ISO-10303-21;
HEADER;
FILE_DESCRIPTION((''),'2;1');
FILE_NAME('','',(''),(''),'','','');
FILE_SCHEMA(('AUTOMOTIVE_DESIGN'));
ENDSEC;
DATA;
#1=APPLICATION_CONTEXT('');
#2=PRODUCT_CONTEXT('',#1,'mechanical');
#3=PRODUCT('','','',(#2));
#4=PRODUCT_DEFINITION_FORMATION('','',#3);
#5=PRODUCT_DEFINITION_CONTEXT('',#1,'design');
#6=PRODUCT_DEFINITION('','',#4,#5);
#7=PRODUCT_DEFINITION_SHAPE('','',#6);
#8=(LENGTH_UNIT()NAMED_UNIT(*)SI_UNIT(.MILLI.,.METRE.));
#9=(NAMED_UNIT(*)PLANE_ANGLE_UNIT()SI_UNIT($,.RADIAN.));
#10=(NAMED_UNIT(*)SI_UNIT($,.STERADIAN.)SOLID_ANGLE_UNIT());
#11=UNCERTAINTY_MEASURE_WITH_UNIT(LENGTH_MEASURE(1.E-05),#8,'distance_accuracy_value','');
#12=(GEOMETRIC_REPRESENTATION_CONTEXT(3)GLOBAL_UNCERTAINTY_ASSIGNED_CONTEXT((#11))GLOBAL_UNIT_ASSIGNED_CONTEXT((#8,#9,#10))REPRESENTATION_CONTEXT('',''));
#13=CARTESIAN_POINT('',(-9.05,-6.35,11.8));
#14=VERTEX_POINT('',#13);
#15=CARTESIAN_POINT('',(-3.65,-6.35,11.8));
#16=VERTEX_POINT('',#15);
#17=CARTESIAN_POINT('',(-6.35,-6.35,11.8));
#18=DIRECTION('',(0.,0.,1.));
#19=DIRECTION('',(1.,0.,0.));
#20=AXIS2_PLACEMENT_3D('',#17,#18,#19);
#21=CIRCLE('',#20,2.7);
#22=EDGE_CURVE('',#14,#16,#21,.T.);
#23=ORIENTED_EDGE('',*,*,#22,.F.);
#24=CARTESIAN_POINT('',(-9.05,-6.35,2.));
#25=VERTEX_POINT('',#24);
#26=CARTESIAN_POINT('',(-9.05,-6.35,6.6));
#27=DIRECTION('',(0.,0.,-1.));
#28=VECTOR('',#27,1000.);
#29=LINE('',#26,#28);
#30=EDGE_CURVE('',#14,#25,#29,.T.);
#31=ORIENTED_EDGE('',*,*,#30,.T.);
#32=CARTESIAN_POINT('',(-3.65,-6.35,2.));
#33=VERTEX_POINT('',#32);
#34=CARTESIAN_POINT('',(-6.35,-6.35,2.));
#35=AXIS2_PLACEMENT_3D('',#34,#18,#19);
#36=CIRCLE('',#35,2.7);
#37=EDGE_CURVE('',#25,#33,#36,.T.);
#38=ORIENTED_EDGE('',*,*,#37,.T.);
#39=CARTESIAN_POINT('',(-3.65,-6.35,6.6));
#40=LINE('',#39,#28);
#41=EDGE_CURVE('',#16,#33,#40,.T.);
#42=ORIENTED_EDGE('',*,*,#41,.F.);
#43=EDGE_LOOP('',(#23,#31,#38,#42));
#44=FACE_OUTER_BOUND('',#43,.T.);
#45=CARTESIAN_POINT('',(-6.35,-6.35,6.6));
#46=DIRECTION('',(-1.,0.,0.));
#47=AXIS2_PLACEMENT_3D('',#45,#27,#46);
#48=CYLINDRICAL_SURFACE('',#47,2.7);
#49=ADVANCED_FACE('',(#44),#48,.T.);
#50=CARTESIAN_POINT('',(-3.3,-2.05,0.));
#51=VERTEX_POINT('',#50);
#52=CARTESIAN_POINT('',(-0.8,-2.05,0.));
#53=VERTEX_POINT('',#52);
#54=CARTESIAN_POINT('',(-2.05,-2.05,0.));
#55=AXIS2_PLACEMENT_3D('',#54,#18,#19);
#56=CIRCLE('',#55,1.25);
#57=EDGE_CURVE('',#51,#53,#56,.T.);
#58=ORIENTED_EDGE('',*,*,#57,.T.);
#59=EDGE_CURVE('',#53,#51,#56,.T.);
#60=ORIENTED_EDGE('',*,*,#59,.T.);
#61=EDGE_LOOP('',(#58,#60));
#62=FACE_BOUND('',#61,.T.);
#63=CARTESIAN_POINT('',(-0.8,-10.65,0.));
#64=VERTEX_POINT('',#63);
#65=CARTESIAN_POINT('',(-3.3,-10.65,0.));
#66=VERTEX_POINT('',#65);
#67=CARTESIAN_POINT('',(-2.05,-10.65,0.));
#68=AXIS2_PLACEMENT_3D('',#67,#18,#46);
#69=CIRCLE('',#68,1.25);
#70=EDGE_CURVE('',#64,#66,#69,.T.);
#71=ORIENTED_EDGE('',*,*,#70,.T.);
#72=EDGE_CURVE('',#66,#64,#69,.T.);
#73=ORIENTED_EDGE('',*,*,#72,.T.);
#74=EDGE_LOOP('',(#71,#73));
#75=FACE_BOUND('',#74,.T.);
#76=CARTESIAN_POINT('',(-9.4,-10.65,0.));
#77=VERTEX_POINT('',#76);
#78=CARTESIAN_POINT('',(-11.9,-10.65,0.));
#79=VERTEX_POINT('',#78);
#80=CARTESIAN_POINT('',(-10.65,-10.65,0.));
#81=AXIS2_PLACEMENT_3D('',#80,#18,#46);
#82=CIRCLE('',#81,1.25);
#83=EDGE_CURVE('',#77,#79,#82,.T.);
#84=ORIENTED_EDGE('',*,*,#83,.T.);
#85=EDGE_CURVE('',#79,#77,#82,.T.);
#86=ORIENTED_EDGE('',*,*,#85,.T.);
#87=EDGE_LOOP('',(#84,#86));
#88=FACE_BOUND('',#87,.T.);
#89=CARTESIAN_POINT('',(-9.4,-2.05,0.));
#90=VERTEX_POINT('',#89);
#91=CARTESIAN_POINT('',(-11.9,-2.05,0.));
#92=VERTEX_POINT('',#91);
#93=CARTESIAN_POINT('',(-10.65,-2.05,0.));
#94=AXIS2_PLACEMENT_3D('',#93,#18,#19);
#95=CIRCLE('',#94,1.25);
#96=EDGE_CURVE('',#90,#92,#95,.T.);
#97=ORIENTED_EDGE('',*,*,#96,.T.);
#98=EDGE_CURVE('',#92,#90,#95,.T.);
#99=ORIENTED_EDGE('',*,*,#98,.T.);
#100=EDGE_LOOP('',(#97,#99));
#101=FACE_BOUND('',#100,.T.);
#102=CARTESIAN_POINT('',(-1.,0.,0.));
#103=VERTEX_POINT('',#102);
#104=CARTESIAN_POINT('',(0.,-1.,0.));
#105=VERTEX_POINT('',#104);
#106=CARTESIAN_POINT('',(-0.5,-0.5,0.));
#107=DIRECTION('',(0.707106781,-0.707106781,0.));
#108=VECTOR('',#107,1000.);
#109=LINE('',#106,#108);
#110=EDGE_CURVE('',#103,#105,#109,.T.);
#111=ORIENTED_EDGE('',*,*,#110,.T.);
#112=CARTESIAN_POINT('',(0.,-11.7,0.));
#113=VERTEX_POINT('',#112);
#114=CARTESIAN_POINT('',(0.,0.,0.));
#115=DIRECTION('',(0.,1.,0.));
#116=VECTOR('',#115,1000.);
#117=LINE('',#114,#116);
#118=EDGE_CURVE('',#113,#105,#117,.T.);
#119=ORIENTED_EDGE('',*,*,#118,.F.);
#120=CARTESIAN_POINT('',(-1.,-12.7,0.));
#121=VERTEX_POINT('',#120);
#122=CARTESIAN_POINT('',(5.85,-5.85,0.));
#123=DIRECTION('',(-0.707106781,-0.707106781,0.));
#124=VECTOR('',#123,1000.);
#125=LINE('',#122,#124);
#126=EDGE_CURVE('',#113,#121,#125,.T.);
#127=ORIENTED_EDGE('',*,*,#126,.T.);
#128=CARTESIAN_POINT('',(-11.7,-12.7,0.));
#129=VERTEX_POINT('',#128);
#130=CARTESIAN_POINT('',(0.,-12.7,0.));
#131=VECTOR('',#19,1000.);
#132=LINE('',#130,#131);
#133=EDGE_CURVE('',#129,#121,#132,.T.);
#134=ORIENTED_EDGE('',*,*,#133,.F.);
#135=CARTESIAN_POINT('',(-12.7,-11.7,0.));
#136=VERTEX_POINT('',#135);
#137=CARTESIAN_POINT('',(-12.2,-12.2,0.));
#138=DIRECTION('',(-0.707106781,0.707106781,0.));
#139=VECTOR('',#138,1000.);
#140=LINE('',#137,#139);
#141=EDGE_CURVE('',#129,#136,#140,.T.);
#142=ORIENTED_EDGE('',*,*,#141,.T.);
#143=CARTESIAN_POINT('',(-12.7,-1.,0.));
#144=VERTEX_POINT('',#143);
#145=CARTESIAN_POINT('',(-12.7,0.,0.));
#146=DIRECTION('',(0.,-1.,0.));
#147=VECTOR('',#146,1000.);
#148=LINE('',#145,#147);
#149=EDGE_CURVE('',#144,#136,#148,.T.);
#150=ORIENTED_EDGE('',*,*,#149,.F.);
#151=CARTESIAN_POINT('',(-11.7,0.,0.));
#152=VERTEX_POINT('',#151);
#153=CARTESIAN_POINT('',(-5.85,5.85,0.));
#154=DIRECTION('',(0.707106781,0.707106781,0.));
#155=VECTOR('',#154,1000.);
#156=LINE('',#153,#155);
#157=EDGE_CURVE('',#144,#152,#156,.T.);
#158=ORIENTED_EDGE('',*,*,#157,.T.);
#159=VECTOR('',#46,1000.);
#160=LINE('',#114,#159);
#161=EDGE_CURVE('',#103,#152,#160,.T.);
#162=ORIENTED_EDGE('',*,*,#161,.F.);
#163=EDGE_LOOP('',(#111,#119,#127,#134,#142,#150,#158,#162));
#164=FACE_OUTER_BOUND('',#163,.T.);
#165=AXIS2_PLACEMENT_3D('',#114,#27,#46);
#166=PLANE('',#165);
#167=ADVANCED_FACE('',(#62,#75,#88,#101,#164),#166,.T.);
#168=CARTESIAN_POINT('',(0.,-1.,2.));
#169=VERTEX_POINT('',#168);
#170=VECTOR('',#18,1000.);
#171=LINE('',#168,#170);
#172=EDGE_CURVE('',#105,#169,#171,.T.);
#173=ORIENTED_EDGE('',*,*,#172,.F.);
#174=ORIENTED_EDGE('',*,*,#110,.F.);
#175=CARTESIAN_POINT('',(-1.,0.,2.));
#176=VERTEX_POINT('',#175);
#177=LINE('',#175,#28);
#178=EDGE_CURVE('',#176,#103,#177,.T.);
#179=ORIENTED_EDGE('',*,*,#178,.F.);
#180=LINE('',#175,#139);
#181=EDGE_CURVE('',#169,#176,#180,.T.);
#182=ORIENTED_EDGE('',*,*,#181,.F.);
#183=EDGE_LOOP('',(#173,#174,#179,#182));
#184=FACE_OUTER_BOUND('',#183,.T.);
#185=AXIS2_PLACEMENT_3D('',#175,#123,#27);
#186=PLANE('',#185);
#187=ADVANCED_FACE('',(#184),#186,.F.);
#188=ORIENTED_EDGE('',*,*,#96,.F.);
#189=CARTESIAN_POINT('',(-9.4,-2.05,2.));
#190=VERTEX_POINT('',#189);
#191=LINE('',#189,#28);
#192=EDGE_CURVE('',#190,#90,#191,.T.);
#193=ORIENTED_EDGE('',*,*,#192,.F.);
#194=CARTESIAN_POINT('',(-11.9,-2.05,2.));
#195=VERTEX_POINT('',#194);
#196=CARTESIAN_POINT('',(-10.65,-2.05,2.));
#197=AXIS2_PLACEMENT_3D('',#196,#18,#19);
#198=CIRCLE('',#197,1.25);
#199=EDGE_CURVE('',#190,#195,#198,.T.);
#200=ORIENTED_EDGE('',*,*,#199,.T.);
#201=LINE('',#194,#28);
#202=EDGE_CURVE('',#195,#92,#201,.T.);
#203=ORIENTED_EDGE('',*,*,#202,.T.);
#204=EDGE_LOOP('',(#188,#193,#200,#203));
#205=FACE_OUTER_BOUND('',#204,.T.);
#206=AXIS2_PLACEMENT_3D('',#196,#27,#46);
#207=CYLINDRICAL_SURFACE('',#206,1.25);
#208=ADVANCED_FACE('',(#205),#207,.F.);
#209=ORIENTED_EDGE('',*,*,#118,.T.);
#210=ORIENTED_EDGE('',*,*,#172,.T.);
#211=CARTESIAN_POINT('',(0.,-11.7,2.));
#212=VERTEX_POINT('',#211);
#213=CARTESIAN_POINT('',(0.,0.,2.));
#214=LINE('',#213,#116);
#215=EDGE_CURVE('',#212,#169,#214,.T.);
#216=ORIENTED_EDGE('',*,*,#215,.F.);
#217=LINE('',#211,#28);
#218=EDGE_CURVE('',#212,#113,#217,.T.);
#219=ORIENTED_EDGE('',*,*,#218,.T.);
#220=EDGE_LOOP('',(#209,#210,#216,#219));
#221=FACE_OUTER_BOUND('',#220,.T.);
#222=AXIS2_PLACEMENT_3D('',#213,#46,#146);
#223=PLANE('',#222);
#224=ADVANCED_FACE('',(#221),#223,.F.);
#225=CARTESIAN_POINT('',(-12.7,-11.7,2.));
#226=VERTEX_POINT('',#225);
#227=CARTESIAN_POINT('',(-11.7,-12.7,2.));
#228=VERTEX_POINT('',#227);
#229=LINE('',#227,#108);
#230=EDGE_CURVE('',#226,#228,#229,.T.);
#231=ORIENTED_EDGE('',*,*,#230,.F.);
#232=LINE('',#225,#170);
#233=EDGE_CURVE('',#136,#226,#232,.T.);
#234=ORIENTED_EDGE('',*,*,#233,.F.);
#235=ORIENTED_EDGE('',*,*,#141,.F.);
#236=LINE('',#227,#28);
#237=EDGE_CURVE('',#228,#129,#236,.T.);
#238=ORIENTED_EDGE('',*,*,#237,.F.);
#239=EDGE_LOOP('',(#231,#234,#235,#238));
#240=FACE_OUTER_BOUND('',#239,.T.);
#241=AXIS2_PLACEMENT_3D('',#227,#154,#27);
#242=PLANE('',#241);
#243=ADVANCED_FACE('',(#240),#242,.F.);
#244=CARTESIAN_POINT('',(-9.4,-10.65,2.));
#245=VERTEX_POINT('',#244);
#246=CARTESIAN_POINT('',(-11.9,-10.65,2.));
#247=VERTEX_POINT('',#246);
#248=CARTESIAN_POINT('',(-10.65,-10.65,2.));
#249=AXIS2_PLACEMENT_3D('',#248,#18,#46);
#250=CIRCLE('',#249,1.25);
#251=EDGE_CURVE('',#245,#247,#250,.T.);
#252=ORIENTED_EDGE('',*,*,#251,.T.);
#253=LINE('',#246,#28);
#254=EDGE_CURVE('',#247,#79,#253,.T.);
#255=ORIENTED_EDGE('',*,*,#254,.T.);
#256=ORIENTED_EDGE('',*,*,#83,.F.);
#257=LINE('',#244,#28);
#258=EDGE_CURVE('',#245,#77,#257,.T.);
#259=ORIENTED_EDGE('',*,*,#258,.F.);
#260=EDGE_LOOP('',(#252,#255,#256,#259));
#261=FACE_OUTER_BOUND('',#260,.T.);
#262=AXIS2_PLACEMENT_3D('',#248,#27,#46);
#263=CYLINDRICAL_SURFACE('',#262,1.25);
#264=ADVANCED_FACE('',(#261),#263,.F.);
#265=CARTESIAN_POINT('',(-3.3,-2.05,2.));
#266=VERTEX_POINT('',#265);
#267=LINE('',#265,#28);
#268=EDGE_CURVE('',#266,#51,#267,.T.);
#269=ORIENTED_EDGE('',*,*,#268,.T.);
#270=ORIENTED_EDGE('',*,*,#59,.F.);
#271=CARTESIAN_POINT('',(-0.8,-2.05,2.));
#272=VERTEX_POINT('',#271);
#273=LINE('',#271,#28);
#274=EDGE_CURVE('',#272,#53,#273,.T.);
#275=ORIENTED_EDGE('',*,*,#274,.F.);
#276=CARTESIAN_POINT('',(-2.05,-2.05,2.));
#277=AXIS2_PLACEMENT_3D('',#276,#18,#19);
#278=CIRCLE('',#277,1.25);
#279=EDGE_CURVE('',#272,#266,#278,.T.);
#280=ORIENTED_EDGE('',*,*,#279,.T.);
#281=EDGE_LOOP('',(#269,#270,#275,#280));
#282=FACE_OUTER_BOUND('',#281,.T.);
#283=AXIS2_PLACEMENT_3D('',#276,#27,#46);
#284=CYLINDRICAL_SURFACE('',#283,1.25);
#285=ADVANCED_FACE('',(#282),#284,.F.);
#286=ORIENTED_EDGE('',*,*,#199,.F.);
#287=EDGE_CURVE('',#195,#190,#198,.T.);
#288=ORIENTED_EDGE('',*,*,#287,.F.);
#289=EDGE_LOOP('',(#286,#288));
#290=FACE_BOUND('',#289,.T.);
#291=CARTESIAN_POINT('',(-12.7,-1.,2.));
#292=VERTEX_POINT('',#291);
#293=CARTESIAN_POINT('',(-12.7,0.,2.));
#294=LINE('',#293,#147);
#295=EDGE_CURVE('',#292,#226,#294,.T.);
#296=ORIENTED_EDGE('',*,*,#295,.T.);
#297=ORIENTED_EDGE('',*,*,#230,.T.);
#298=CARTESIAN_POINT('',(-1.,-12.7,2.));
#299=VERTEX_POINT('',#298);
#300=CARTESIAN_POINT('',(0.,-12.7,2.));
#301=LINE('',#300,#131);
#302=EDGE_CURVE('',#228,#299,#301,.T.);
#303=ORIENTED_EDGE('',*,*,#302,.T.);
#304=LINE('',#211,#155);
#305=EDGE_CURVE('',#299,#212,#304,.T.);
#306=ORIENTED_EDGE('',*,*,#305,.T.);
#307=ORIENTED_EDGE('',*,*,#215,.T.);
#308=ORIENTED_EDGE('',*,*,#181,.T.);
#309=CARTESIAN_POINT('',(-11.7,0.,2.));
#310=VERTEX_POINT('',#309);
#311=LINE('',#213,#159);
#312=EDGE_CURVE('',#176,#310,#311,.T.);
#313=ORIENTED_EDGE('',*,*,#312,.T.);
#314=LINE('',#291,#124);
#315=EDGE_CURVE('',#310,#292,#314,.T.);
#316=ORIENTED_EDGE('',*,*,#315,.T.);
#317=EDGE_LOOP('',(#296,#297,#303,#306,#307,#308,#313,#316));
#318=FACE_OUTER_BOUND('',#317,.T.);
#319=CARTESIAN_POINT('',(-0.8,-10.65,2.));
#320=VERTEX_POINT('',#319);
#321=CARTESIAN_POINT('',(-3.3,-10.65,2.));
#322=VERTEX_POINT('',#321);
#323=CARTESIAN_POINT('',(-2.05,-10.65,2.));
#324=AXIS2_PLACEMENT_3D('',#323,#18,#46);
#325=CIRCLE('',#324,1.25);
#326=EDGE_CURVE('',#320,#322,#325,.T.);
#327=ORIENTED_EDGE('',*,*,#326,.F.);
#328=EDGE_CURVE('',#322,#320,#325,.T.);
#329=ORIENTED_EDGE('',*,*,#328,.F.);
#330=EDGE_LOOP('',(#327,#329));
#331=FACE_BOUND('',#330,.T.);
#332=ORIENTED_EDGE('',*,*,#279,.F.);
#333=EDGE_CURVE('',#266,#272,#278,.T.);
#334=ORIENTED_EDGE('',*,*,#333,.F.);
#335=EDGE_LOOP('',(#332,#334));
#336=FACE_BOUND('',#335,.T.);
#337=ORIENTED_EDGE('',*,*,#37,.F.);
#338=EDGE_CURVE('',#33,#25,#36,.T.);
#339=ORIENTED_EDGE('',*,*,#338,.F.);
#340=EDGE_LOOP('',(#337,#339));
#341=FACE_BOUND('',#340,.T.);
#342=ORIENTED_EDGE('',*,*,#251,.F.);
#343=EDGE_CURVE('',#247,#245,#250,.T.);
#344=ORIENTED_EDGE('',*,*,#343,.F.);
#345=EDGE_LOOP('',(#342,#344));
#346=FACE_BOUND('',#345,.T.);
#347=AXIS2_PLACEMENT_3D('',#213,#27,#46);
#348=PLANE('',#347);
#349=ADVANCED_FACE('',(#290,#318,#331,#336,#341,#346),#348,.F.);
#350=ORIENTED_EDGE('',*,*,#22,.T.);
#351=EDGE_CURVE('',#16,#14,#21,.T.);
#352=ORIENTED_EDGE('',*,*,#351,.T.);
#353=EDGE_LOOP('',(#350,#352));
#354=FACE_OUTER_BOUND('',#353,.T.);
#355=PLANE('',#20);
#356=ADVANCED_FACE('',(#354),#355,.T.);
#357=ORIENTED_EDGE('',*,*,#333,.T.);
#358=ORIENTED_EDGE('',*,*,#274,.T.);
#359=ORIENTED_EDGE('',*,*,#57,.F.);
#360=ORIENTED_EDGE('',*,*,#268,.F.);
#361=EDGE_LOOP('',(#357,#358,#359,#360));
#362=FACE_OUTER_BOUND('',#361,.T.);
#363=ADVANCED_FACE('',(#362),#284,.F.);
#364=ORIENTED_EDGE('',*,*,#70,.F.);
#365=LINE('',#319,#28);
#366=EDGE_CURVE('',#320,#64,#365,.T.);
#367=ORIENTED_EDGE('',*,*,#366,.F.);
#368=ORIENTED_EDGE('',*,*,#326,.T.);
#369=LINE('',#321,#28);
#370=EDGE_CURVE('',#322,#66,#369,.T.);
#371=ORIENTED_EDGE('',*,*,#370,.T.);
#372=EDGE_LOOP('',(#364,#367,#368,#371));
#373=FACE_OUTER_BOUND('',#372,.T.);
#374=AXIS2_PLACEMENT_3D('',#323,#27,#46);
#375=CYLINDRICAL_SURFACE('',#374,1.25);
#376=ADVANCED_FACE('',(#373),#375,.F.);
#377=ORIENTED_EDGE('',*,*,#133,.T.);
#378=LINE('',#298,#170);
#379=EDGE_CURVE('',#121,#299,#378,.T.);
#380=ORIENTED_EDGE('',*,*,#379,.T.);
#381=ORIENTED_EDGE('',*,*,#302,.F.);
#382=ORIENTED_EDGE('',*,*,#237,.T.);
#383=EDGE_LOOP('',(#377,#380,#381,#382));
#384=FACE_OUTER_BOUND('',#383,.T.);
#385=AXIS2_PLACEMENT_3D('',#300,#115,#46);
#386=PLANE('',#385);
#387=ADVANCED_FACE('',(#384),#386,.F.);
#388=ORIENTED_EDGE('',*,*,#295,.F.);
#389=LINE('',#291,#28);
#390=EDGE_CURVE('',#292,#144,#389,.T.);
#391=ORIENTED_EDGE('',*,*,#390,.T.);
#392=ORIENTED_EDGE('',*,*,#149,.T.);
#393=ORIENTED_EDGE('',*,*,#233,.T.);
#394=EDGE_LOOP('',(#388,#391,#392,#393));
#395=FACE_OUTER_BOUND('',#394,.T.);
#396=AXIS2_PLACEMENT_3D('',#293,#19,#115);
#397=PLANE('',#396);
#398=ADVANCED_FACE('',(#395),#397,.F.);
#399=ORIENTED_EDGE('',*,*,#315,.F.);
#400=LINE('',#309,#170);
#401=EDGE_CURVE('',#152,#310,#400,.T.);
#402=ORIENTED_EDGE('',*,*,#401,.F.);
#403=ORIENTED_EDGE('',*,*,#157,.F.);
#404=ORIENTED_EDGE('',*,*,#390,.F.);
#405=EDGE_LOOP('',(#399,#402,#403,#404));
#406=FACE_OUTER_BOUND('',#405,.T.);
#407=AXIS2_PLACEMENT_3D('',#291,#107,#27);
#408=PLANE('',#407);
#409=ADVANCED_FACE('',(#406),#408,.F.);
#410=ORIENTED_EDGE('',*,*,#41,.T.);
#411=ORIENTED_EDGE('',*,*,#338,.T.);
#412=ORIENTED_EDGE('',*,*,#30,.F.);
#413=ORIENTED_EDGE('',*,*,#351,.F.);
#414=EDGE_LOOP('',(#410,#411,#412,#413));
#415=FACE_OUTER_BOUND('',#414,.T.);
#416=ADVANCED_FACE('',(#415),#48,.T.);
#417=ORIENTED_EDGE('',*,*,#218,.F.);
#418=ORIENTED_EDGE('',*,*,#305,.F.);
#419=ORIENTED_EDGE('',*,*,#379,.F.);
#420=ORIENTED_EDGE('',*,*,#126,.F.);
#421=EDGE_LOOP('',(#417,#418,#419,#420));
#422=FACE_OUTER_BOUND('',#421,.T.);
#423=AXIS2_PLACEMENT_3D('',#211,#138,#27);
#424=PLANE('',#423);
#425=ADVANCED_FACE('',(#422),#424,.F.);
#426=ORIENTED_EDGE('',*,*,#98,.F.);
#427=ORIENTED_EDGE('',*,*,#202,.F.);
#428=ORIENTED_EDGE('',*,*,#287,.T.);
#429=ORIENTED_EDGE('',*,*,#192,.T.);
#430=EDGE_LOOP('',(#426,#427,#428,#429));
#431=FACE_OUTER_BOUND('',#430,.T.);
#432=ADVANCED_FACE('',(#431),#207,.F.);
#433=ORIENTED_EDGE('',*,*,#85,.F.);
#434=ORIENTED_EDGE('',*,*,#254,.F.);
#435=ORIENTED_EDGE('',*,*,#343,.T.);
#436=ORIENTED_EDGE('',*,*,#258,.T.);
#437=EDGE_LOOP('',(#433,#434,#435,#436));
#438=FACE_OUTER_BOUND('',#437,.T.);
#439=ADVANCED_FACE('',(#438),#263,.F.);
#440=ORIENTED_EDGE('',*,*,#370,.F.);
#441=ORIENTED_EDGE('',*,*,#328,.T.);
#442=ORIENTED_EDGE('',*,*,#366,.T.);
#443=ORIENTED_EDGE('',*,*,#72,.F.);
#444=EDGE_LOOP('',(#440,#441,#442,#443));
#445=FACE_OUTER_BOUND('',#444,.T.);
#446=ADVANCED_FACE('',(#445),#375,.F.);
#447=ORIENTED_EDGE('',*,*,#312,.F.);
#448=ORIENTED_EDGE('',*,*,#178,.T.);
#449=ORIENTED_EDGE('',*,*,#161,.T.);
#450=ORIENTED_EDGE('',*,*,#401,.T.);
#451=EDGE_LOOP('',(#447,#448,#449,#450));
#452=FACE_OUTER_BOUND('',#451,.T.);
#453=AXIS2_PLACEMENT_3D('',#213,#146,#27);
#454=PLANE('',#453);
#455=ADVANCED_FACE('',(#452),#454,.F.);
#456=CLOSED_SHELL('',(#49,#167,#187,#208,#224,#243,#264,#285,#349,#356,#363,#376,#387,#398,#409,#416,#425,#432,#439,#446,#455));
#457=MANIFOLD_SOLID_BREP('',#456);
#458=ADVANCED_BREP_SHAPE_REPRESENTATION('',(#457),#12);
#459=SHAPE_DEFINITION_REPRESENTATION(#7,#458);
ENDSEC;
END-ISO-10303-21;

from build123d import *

# Parameters (mm, degrees)
SKETCH1_W           = 12.7
SKETCH1_H           = 12.7
SKETCH1_R           = 1.25
BOSS_EXTRUDE1_DEPTH = 2
CHAMFER1_SIZE       = 1
SKETCH2_R           = 2.7
BOSS_EXTRUDE2_DEPTH = 4.6
SKETCH3_R           = 2.7
BOSS_EXTRUDE3_DEPTH = 5.2


with BuildPart() as part:
    # Sketch1 → Boss-Extrude1 (new body)
    with BuildSketch(Plane.XY):
        with Locations((-6.35, -6.35)):
            Rectangle(SKETCH1_W, SKETCH1_H)
        with Locations((-10.65, -2.05)):
            Circle(SKETCH1_R, mode=Mode.SUBTRACT)
        with Locations((-2.05, -2.05)):
            Circle(SKETCH1_R, mode=Mode.SUBTRACT)
        with Locations(Location((-2.05, -10.65, 0), (0, 0, 180))):
            Circle(SKETCH1_R, mode=Mode.SUBTRACT)
        with Locations(Location((-10.65, -10.65, 0), (0, 0, 180))):
            Circle(SKETCH1_R, mode=Mode.SUBTRACT)
    extrude(amount=BOSS_EXTRUDE1_DEPTH)

    # Chamfer1
    chamfer1_edges = [part.edges().sort_by_distance(p)[0] for p in [
        (0, -12.7, 1),
        (-12.7, -12.7, 1),
        (-12.7, 0, 1),
        (0, 0, 1),
    ]]
    chamfer(chamfer1_edges, length=CHAMFER1_SIZE)

    # Sketch2 → Boss-Extrude2 (add)
    with BuildSketch(Plane.XY.offset(2)):
        with Locations((-6.35, -6.35)):
            Circle(SKETCH2_R)
    extrude(amount=BOSS_EXTRUDE2_DEPTH)

    # Sketch3 → Boss-Extrude3 (add)
    with BuildSketch(Plane.XY.offset(6.6)):
        with Locations((-6.35, -6.35)):
            Circle(SKETCH3_R)
    extrude(amount=BOSS_EXTRUDE3_DEPTH)


solid = part.part
